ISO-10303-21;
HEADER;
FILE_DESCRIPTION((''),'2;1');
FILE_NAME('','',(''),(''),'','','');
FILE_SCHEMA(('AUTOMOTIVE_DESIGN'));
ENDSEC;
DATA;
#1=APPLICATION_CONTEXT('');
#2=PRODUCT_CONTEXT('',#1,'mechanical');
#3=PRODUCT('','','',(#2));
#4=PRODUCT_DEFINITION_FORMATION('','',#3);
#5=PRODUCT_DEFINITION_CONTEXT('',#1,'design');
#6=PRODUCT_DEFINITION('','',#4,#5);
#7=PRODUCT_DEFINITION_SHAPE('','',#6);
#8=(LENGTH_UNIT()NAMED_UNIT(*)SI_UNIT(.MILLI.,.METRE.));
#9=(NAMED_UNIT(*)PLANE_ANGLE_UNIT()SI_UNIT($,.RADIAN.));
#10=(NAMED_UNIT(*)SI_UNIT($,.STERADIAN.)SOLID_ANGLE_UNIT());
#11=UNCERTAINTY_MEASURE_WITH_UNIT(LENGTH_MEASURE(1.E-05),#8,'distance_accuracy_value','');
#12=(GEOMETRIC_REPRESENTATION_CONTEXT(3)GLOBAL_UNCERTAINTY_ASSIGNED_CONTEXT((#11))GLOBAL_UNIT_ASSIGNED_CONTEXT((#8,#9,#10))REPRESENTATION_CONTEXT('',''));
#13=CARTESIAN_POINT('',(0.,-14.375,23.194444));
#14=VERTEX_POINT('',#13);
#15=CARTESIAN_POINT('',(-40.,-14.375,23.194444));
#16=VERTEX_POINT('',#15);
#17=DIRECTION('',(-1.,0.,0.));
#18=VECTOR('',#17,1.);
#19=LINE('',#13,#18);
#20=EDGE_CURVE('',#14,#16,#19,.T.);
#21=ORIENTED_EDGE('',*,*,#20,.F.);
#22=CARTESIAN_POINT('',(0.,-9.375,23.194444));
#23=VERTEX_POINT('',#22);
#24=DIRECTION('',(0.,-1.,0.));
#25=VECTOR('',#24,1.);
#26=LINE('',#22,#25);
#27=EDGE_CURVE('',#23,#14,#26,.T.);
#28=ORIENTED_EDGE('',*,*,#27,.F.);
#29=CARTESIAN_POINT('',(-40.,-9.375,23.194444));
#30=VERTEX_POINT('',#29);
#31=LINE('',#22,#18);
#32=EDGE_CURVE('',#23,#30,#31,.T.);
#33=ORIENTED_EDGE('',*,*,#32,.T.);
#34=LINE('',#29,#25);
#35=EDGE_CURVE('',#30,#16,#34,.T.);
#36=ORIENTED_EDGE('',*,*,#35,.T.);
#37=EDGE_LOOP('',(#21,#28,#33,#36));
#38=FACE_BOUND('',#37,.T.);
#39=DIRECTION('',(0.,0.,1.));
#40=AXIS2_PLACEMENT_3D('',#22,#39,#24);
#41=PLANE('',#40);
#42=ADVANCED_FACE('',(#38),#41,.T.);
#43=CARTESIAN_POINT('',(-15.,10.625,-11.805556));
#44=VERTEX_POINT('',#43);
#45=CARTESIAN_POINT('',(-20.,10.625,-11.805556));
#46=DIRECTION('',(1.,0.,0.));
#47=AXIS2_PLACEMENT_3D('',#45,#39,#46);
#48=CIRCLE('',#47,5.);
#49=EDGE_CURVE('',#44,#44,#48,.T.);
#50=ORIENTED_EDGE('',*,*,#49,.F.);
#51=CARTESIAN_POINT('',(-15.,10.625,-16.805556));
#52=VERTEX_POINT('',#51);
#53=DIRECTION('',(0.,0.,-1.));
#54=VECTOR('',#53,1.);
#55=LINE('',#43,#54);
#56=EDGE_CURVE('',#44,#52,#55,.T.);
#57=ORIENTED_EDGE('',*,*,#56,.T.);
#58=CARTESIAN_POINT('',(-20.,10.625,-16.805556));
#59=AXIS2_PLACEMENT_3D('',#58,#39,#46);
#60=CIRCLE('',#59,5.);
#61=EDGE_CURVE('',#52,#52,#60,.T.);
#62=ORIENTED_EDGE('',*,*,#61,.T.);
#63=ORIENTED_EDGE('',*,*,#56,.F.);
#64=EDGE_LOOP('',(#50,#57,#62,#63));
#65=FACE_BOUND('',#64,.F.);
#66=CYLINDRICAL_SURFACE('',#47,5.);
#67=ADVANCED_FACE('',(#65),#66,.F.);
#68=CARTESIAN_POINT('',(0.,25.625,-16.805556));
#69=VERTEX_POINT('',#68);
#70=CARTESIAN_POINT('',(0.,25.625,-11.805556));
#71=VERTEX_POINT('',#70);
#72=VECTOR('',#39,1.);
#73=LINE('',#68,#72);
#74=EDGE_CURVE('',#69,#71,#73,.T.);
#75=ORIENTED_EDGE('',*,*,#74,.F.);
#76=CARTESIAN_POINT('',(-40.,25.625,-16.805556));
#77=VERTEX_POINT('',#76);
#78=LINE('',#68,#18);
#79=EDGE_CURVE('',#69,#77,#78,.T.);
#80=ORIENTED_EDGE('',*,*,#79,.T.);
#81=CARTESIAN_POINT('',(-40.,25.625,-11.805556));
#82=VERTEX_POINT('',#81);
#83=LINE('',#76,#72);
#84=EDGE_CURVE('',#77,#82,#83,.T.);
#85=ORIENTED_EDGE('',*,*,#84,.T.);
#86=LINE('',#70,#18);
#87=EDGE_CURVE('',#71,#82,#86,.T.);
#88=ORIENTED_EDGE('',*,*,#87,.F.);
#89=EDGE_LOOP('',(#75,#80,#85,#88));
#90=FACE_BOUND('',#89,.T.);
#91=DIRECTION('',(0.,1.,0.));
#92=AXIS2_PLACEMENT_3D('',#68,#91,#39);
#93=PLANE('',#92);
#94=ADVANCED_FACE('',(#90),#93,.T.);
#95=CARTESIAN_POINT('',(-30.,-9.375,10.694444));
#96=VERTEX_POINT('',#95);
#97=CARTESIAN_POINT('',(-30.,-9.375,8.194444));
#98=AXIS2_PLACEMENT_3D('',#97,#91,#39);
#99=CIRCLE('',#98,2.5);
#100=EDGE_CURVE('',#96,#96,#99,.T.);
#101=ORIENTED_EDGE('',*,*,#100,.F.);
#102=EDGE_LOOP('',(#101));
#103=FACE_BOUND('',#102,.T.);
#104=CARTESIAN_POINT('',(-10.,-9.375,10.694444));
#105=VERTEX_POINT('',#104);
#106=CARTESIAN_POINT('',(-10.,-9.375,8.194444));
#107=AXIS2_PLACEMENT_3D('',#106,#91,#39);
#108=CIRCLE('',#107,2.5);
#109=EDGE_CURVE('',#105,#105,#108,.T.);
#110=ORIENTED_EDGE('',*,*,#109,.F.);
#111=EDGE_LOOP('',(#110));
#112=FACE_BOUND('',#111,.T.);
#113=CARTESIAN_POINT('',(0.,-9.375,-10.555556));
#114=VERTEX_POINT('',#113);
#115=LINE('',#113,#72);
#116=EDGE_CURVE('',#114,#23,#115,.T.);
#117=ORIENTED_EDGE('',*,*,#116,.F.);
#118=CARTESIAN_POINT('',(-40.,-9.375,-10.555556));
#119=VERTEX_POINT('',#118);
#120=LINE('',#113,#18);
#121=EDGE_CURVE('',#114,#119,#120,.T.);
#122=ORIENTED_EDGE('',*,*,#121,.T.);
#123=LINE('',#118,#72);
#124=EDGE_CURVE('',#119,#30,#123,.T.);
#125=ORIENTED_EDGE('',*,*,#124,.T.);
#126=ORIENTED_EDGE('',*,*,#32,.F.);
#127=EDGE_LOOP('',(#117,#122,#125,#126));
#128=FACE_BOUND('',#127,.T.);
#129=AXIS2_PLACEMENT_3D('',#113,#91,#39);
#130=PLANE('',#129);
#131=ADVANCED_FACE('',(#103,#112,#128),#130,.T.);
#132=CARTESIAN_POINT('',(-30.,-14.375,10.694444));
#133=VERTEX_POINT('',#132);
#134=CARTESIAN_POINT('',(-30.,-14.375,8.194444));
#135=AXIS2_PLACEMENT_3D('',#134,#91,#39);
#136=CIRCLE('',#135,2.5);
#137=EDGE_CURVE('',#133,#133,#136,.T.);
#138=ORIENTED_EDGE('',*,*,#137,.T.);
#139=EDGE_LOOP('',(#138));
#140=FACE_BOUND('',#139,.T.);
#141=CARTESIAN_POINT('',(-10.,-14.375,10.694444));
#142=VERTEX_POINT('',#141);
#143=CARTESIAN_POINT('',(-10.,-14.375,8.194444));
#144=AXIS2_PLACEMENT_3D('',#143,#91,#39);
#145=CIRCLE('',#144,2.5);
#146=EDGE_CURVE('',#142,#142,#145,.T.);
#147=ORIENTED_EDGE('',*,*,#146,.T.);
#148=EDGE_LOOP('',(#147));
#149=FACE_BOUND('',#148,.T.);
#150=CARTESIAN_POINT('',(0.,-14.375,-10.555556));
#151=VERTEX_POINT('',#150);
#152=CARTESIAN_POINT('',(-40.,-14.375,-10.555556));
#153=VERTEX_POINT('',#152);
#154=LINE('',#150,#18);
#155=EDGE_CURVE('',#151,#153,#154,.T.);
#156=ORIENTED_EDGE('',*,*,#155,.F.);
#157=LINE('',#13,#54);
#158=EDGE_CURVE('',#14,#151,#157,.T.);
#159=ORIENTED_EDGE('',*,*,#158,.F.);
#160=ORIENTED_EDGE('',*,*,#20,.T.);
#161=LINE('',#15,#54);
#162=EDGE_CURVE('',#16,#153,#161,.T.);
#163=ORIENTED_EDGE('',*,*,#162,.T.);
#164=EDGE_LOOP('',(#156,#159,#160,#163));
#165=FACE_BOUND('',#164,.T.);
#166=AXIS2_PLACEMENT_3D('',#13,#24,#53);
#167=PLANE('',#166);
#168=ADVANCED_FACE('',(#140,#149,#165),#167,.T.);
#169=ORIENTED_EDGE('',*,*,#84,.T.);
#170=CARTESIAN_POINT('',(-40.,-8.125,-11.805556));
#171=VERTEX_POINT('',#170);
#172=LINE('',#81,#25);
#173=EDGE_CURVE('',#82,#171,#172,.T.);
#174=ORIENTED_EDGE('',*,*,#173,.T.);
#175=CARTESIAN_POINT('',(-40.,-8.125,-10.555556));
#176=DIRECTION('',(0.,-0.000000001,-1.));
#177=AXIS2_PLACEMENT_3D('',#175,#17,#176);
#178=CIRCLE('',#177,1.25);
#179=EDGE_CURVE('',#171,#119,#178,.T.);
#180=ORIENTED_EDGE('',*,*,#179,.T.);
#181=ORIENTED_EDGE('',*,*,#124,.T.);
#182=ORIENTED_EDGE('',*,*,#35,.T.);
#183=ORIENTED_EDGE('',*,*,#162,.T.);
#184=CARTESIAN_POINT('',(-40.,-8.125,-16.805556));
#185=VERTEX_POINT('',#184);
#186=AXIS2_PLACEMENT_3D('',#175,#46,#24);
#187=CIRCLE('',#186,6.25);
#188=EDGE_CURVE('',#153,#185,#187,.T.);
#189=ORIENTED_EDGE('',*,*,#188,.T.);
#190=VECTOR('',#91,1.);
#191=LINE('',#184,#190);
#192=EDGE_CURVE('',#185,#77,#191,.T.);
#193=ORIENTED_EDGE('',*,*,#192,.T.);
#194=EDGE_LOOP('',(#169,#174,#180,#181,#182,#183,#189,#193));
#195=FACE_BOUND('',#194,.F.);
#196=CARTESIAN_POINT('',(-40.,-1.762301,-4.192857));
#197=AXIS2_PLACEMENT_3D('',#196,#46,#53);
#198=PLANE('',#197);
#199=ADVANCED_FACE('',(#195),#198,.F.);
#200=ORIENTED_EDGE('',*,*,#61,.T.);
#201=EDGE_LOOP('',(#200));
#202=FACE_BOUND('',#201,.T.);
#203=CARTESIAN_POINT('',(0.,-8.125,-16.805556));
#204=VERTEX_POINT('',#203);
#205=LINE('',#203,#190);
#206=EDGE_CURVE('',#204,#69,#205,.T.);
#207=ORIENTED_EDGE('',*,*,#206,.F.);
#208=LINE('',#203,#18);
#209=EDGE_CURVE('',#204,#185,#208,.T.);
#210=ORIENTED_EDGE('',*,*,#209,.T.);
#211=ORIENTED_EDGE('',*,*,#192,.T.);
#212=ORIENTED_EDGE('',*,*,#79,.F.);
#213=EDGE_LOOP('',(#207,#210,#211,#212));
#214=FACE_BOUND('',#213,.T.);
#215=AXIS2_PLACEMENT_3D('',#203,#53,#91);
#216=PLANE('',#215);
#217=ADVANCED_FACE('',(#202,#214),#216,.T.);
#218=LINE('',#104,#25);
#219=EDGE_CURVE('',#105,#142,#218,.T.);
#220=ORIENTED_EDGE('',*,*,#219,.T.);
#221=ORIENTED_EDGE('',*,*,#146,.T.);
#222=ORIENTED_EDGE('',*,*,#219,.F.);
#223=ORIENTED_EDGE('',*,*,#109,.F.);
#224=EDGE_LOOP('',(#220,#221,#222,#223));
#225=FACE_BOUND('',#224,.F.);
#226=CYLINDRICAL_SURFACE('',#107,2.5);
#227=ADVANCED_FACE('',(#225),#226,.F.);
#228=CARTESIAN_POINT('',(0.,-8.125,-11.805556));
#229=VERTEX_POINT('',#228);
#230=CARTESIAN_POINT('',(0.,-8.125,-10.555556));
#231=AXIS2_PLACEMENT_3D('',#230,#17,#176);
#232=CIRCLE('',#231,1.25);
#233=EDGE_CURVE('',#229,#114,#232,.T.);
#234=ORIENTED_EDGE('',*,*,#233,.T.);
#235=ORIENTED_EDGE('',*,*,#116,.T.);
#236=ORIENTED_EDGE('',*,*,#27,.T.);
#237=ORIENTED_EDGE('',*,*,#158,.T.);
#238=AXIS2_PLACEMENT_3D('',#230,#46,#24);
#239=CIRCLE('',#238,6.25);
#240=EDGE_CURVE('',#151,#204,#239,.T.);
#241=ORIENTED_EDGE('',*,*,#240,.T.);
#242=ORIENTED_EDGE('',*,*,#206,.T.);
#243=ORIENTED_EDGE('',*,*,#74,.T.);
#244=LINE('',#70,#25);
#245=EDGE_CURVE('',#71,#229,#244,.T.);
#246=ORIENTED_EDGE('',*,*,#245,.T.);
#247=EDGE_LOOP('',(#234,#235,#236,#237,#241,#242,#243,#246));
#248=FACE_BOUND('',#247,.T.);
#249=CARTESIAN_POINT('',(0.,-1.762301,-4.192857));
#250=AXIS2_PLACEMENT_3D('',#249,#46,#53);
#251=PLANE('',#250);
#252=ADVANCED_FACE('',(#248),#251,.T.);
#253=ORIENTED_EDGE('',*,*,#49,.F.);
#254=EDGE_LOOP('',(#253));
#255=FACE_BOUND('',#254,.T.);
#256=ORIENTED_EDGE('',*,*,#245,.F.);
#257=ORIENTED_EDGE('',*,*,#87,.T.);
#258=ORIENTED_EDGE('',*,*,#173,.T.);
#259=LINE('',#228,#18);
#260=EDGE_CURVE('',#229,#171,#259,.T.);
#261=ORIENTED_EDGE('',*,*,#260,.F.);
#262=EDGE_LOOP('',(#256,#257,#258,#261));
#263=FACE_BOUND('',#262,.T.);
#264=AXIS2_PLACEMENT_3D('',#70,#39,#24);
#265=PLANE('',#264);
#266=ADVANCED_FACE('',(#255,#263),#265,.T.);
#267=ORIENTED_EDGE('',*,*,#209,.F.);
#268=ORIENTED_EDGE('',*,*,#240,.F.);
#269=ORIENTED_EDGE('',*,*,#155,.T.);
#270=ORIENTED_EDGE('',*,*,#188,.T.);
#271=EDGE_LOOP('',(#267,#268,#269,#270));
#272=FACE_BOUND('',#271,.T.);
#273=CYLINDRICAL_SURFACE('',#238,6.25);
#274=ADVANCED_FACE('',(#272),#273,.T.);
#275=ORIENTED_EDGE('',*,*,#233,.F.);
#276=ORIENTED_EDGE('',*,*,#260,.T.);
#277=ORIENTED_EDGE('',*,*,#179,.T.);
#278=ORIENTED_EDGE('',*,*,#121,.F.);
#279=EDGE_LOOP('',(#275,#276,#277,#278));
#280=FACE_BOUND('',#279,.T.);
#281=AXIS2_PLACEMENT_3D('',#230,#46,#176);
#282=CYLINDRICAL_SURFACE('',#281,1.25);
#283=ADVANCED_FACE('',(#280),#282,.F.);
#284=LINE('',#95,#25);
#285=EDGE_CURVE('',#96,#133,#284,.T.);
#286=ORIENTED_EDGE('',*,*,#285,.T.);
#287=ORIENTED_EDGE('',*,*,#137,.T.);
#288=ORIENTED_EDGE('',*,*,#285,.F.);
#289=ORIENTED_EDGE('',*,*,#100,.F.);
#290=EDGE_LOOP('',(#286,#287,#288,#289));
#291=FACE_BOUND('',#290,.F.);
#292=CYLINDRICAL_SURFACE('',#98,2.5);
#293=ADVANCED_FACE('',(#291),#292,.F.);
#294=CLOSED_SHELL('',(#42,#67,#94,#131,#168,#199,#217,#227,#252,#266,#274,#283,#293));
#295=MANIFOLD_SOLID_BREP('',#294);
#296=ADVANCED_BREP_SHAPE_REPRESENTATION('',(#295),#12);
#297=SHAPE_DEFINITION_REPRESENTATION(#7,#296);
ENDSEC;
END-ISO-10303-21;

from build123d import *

# Parameters (mm, degrees)
BOSS_EXTRUDE1_DEPTH = 40
SKETCH2_R           = 5
CUT_EXTRUDE1_DEPTH  = 40
SKETCH3_R           = 2.5
CUT_EXTRUDE2_DEPTH  = 40


with BuildPart() as part:
    # Sketch1 → Boss-Extrude1 (new body)
    with BuildSketch(Plane(origin=(0, 0, 0), x_dir=(0, 0, -1), z_dir=(1, 0, 0))):
        with BuildLine():
            Line((11.805555556, 25.625), (11.805555556, -8.125))
            ThreePointArc((11.805555556, -8.125), (11.439439032, -9.008883476), (10.555555556, -9.375))
            Line((10.555555556, -9.375), (-23.194444444, -9.375))
            Line((-23.194444444, -9.375), (-23.194444444, -14.375))
            Line((-23.194444444, -14.375), (10.555555556, -14.375))
            ThreePointArc((10.555555556, -14.375), (14.974972938, -12.544417382), (16.805555556, -8.125))
            Line((16.805555556, -8.125), (16.805555556, 25.625))
            Line((16.805555556, 25.625), (11.805555556, 25.625))
        make_face()
    extrude(amount=-BOSS_EXTRUDE1_DEPTH)

    # Sketch2 → Cut-Extrude1 (cut)
    with BuildSketch(Plane.XY.offset(-11.805555556)):
        with Locations((-20, 10.625)):
            Circle(SKETCH2_R)
    extrude(amount=-CUT_EXTRUDE1_DEPTH, mode=Mode.SUBTRACT)

    # Sketch3 → Cut-Extrude2 (cut)
    with BuildSketch(Plane(origin=(0, -9.375, 0), x_dir=(1, 0, 0), z_dir=(0, 1, 0))):
        with Locations(Location((-30, -8.194444444, 0), (0, 0, 270))):
            Circle(SKETCH3_R)
        with Locations(Location((-10, -8.194444444, 0), (0, 0, 270))):
            Circle(SKETCH3_R)
    extrude(amount=-CUT_EXTRUDE2_DEPTH, mode=Mode.SUBTRACT)


solid = part.part
